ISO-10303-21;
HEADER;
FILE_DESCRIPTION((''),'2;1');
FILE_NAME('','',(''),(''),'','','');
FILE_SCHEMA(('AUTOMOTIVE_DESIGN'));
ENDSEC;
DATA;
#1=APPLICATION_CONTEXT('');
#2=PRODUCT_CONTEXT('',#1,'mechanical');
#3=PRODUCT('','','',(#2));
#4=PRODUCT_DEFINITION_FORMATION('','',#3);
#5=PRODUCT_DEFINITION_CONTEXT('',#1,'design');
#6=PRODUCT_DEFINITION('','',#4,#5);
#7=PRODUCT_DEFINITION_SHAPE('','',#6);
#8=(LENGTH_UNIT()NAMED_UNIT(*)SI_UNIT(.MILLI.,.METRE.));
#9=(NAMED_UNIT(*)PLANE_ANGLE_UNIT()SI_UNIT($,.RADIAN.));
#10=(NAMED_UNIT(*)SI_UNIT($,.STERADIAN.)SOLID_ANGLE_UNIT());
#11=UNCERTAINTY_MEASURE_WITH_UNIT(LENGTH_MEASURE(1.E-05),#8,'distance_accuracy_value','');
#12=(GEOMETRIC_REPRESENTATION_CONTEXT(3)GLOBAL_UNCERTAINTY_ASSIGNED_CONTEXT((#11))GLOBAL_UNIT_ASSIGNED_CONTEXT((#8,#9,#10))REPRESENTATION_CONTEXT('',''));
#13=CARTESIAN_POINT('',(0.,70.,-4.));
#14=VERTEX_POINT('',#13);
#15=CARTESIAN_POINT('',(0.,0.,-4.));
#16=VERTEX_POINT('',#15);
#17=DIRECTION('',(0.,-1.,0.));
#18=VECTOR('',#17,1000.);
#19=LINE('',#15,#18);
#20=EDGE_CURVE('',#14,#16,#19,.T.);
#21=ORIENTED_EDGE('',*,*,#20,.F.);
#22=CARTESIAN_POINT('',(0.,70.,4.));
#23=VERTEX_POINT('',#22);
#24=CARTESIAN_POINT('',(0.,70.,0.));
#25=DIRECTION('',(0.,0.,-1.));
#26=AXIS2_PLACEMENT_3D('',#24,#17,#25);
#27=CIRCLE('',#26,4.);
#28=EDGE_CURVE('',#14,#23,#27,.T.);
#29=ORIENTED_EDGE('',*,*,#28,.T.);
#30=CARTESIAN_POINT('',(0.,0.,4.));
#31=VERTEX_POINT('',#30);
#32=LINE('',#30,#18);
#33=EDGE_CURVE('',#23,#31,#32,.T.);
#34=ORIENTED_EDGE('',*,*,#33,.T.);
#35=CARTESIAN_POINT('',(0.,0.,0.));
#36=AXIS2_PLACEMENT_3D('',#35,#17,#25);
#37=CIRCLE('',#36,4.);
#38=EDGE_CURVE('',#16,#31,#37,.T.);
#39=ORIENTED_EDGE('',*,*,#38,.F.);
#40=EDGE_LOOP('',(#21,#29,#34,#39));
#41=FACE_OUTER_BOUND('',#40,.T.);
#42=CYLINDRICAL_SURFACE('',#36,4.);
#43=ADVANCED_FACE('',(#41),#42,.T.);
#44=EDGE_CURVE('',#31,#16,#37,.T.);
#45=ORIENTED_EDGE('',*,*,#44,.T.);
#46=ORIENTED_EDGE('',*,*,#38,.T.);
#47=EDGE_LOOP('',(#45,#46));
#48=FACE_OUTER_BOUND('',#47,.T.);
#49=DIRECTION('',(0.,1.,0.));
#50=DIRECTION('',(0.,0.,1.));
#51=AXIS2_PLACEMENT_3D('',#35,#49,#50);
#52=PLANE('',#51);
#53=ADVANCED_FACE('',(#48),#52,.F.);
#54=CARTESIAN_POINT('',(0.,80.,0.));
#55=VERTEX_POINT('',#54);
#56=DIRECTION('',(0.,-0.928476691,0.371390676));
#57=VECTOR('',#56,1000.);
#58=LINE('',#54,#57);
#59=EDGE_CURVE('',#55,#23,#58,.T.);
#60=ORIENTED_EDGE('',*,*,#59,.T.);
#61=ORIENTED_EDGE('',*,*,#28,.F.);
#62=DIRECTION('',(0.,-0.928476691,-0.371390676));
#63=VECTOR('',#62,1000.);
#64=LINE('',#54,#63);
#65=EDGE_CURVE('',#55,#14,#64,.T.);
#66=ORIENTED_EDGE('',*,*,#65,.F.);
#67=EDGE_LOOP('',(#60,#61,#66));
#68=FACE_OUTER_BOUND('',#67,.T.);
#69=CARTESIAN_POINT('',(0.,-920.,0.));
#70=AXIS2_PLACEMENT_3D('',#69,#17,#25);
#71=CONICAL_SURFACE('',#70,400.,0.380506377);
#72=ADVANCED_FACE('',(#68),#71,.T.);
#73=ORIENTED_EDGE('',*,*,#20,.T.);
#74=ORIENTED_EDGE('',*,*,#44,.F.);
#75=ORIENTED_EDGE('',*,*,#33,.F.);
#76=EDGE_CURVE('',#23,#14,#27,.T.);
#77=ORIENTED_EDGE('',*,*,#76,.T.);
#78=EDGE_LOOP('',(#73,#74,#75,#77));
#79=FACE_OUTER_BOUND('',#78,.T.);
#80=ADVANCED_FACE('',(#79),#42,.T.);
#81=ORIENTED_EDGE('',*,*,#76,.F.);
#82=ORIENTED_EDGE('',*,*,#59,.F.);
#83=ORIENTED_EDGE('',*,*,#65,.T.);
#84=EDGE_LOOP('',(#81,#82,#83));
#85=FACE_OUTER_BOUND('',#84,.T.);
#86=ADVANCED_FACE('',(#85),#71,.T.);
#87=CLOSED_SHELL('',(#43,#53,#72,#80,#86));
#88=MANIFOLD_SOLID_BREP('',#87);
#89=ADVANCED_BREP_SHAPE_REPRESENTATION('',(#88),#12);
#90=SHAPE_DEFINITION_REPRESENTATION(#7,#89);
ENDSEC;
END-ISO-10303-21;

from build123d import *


with BuildPart() as part:
    # 草图1 → 旋转1 (revolve)
    with BuildSketch(Plane.XY, mode=Mode.PRIVATE) as revolve_1_sk:
        Polygon((0, 0), (0, 80), (-4, 70), (-4, 0), align=None)
    revolve(revolve_1_sk.sketch.rotate(Axis((0, 0, 0), (0, 1, 0)), 270), axis=Axis((0, 0, 0), (0, 1, 0)))


solid = part.part
